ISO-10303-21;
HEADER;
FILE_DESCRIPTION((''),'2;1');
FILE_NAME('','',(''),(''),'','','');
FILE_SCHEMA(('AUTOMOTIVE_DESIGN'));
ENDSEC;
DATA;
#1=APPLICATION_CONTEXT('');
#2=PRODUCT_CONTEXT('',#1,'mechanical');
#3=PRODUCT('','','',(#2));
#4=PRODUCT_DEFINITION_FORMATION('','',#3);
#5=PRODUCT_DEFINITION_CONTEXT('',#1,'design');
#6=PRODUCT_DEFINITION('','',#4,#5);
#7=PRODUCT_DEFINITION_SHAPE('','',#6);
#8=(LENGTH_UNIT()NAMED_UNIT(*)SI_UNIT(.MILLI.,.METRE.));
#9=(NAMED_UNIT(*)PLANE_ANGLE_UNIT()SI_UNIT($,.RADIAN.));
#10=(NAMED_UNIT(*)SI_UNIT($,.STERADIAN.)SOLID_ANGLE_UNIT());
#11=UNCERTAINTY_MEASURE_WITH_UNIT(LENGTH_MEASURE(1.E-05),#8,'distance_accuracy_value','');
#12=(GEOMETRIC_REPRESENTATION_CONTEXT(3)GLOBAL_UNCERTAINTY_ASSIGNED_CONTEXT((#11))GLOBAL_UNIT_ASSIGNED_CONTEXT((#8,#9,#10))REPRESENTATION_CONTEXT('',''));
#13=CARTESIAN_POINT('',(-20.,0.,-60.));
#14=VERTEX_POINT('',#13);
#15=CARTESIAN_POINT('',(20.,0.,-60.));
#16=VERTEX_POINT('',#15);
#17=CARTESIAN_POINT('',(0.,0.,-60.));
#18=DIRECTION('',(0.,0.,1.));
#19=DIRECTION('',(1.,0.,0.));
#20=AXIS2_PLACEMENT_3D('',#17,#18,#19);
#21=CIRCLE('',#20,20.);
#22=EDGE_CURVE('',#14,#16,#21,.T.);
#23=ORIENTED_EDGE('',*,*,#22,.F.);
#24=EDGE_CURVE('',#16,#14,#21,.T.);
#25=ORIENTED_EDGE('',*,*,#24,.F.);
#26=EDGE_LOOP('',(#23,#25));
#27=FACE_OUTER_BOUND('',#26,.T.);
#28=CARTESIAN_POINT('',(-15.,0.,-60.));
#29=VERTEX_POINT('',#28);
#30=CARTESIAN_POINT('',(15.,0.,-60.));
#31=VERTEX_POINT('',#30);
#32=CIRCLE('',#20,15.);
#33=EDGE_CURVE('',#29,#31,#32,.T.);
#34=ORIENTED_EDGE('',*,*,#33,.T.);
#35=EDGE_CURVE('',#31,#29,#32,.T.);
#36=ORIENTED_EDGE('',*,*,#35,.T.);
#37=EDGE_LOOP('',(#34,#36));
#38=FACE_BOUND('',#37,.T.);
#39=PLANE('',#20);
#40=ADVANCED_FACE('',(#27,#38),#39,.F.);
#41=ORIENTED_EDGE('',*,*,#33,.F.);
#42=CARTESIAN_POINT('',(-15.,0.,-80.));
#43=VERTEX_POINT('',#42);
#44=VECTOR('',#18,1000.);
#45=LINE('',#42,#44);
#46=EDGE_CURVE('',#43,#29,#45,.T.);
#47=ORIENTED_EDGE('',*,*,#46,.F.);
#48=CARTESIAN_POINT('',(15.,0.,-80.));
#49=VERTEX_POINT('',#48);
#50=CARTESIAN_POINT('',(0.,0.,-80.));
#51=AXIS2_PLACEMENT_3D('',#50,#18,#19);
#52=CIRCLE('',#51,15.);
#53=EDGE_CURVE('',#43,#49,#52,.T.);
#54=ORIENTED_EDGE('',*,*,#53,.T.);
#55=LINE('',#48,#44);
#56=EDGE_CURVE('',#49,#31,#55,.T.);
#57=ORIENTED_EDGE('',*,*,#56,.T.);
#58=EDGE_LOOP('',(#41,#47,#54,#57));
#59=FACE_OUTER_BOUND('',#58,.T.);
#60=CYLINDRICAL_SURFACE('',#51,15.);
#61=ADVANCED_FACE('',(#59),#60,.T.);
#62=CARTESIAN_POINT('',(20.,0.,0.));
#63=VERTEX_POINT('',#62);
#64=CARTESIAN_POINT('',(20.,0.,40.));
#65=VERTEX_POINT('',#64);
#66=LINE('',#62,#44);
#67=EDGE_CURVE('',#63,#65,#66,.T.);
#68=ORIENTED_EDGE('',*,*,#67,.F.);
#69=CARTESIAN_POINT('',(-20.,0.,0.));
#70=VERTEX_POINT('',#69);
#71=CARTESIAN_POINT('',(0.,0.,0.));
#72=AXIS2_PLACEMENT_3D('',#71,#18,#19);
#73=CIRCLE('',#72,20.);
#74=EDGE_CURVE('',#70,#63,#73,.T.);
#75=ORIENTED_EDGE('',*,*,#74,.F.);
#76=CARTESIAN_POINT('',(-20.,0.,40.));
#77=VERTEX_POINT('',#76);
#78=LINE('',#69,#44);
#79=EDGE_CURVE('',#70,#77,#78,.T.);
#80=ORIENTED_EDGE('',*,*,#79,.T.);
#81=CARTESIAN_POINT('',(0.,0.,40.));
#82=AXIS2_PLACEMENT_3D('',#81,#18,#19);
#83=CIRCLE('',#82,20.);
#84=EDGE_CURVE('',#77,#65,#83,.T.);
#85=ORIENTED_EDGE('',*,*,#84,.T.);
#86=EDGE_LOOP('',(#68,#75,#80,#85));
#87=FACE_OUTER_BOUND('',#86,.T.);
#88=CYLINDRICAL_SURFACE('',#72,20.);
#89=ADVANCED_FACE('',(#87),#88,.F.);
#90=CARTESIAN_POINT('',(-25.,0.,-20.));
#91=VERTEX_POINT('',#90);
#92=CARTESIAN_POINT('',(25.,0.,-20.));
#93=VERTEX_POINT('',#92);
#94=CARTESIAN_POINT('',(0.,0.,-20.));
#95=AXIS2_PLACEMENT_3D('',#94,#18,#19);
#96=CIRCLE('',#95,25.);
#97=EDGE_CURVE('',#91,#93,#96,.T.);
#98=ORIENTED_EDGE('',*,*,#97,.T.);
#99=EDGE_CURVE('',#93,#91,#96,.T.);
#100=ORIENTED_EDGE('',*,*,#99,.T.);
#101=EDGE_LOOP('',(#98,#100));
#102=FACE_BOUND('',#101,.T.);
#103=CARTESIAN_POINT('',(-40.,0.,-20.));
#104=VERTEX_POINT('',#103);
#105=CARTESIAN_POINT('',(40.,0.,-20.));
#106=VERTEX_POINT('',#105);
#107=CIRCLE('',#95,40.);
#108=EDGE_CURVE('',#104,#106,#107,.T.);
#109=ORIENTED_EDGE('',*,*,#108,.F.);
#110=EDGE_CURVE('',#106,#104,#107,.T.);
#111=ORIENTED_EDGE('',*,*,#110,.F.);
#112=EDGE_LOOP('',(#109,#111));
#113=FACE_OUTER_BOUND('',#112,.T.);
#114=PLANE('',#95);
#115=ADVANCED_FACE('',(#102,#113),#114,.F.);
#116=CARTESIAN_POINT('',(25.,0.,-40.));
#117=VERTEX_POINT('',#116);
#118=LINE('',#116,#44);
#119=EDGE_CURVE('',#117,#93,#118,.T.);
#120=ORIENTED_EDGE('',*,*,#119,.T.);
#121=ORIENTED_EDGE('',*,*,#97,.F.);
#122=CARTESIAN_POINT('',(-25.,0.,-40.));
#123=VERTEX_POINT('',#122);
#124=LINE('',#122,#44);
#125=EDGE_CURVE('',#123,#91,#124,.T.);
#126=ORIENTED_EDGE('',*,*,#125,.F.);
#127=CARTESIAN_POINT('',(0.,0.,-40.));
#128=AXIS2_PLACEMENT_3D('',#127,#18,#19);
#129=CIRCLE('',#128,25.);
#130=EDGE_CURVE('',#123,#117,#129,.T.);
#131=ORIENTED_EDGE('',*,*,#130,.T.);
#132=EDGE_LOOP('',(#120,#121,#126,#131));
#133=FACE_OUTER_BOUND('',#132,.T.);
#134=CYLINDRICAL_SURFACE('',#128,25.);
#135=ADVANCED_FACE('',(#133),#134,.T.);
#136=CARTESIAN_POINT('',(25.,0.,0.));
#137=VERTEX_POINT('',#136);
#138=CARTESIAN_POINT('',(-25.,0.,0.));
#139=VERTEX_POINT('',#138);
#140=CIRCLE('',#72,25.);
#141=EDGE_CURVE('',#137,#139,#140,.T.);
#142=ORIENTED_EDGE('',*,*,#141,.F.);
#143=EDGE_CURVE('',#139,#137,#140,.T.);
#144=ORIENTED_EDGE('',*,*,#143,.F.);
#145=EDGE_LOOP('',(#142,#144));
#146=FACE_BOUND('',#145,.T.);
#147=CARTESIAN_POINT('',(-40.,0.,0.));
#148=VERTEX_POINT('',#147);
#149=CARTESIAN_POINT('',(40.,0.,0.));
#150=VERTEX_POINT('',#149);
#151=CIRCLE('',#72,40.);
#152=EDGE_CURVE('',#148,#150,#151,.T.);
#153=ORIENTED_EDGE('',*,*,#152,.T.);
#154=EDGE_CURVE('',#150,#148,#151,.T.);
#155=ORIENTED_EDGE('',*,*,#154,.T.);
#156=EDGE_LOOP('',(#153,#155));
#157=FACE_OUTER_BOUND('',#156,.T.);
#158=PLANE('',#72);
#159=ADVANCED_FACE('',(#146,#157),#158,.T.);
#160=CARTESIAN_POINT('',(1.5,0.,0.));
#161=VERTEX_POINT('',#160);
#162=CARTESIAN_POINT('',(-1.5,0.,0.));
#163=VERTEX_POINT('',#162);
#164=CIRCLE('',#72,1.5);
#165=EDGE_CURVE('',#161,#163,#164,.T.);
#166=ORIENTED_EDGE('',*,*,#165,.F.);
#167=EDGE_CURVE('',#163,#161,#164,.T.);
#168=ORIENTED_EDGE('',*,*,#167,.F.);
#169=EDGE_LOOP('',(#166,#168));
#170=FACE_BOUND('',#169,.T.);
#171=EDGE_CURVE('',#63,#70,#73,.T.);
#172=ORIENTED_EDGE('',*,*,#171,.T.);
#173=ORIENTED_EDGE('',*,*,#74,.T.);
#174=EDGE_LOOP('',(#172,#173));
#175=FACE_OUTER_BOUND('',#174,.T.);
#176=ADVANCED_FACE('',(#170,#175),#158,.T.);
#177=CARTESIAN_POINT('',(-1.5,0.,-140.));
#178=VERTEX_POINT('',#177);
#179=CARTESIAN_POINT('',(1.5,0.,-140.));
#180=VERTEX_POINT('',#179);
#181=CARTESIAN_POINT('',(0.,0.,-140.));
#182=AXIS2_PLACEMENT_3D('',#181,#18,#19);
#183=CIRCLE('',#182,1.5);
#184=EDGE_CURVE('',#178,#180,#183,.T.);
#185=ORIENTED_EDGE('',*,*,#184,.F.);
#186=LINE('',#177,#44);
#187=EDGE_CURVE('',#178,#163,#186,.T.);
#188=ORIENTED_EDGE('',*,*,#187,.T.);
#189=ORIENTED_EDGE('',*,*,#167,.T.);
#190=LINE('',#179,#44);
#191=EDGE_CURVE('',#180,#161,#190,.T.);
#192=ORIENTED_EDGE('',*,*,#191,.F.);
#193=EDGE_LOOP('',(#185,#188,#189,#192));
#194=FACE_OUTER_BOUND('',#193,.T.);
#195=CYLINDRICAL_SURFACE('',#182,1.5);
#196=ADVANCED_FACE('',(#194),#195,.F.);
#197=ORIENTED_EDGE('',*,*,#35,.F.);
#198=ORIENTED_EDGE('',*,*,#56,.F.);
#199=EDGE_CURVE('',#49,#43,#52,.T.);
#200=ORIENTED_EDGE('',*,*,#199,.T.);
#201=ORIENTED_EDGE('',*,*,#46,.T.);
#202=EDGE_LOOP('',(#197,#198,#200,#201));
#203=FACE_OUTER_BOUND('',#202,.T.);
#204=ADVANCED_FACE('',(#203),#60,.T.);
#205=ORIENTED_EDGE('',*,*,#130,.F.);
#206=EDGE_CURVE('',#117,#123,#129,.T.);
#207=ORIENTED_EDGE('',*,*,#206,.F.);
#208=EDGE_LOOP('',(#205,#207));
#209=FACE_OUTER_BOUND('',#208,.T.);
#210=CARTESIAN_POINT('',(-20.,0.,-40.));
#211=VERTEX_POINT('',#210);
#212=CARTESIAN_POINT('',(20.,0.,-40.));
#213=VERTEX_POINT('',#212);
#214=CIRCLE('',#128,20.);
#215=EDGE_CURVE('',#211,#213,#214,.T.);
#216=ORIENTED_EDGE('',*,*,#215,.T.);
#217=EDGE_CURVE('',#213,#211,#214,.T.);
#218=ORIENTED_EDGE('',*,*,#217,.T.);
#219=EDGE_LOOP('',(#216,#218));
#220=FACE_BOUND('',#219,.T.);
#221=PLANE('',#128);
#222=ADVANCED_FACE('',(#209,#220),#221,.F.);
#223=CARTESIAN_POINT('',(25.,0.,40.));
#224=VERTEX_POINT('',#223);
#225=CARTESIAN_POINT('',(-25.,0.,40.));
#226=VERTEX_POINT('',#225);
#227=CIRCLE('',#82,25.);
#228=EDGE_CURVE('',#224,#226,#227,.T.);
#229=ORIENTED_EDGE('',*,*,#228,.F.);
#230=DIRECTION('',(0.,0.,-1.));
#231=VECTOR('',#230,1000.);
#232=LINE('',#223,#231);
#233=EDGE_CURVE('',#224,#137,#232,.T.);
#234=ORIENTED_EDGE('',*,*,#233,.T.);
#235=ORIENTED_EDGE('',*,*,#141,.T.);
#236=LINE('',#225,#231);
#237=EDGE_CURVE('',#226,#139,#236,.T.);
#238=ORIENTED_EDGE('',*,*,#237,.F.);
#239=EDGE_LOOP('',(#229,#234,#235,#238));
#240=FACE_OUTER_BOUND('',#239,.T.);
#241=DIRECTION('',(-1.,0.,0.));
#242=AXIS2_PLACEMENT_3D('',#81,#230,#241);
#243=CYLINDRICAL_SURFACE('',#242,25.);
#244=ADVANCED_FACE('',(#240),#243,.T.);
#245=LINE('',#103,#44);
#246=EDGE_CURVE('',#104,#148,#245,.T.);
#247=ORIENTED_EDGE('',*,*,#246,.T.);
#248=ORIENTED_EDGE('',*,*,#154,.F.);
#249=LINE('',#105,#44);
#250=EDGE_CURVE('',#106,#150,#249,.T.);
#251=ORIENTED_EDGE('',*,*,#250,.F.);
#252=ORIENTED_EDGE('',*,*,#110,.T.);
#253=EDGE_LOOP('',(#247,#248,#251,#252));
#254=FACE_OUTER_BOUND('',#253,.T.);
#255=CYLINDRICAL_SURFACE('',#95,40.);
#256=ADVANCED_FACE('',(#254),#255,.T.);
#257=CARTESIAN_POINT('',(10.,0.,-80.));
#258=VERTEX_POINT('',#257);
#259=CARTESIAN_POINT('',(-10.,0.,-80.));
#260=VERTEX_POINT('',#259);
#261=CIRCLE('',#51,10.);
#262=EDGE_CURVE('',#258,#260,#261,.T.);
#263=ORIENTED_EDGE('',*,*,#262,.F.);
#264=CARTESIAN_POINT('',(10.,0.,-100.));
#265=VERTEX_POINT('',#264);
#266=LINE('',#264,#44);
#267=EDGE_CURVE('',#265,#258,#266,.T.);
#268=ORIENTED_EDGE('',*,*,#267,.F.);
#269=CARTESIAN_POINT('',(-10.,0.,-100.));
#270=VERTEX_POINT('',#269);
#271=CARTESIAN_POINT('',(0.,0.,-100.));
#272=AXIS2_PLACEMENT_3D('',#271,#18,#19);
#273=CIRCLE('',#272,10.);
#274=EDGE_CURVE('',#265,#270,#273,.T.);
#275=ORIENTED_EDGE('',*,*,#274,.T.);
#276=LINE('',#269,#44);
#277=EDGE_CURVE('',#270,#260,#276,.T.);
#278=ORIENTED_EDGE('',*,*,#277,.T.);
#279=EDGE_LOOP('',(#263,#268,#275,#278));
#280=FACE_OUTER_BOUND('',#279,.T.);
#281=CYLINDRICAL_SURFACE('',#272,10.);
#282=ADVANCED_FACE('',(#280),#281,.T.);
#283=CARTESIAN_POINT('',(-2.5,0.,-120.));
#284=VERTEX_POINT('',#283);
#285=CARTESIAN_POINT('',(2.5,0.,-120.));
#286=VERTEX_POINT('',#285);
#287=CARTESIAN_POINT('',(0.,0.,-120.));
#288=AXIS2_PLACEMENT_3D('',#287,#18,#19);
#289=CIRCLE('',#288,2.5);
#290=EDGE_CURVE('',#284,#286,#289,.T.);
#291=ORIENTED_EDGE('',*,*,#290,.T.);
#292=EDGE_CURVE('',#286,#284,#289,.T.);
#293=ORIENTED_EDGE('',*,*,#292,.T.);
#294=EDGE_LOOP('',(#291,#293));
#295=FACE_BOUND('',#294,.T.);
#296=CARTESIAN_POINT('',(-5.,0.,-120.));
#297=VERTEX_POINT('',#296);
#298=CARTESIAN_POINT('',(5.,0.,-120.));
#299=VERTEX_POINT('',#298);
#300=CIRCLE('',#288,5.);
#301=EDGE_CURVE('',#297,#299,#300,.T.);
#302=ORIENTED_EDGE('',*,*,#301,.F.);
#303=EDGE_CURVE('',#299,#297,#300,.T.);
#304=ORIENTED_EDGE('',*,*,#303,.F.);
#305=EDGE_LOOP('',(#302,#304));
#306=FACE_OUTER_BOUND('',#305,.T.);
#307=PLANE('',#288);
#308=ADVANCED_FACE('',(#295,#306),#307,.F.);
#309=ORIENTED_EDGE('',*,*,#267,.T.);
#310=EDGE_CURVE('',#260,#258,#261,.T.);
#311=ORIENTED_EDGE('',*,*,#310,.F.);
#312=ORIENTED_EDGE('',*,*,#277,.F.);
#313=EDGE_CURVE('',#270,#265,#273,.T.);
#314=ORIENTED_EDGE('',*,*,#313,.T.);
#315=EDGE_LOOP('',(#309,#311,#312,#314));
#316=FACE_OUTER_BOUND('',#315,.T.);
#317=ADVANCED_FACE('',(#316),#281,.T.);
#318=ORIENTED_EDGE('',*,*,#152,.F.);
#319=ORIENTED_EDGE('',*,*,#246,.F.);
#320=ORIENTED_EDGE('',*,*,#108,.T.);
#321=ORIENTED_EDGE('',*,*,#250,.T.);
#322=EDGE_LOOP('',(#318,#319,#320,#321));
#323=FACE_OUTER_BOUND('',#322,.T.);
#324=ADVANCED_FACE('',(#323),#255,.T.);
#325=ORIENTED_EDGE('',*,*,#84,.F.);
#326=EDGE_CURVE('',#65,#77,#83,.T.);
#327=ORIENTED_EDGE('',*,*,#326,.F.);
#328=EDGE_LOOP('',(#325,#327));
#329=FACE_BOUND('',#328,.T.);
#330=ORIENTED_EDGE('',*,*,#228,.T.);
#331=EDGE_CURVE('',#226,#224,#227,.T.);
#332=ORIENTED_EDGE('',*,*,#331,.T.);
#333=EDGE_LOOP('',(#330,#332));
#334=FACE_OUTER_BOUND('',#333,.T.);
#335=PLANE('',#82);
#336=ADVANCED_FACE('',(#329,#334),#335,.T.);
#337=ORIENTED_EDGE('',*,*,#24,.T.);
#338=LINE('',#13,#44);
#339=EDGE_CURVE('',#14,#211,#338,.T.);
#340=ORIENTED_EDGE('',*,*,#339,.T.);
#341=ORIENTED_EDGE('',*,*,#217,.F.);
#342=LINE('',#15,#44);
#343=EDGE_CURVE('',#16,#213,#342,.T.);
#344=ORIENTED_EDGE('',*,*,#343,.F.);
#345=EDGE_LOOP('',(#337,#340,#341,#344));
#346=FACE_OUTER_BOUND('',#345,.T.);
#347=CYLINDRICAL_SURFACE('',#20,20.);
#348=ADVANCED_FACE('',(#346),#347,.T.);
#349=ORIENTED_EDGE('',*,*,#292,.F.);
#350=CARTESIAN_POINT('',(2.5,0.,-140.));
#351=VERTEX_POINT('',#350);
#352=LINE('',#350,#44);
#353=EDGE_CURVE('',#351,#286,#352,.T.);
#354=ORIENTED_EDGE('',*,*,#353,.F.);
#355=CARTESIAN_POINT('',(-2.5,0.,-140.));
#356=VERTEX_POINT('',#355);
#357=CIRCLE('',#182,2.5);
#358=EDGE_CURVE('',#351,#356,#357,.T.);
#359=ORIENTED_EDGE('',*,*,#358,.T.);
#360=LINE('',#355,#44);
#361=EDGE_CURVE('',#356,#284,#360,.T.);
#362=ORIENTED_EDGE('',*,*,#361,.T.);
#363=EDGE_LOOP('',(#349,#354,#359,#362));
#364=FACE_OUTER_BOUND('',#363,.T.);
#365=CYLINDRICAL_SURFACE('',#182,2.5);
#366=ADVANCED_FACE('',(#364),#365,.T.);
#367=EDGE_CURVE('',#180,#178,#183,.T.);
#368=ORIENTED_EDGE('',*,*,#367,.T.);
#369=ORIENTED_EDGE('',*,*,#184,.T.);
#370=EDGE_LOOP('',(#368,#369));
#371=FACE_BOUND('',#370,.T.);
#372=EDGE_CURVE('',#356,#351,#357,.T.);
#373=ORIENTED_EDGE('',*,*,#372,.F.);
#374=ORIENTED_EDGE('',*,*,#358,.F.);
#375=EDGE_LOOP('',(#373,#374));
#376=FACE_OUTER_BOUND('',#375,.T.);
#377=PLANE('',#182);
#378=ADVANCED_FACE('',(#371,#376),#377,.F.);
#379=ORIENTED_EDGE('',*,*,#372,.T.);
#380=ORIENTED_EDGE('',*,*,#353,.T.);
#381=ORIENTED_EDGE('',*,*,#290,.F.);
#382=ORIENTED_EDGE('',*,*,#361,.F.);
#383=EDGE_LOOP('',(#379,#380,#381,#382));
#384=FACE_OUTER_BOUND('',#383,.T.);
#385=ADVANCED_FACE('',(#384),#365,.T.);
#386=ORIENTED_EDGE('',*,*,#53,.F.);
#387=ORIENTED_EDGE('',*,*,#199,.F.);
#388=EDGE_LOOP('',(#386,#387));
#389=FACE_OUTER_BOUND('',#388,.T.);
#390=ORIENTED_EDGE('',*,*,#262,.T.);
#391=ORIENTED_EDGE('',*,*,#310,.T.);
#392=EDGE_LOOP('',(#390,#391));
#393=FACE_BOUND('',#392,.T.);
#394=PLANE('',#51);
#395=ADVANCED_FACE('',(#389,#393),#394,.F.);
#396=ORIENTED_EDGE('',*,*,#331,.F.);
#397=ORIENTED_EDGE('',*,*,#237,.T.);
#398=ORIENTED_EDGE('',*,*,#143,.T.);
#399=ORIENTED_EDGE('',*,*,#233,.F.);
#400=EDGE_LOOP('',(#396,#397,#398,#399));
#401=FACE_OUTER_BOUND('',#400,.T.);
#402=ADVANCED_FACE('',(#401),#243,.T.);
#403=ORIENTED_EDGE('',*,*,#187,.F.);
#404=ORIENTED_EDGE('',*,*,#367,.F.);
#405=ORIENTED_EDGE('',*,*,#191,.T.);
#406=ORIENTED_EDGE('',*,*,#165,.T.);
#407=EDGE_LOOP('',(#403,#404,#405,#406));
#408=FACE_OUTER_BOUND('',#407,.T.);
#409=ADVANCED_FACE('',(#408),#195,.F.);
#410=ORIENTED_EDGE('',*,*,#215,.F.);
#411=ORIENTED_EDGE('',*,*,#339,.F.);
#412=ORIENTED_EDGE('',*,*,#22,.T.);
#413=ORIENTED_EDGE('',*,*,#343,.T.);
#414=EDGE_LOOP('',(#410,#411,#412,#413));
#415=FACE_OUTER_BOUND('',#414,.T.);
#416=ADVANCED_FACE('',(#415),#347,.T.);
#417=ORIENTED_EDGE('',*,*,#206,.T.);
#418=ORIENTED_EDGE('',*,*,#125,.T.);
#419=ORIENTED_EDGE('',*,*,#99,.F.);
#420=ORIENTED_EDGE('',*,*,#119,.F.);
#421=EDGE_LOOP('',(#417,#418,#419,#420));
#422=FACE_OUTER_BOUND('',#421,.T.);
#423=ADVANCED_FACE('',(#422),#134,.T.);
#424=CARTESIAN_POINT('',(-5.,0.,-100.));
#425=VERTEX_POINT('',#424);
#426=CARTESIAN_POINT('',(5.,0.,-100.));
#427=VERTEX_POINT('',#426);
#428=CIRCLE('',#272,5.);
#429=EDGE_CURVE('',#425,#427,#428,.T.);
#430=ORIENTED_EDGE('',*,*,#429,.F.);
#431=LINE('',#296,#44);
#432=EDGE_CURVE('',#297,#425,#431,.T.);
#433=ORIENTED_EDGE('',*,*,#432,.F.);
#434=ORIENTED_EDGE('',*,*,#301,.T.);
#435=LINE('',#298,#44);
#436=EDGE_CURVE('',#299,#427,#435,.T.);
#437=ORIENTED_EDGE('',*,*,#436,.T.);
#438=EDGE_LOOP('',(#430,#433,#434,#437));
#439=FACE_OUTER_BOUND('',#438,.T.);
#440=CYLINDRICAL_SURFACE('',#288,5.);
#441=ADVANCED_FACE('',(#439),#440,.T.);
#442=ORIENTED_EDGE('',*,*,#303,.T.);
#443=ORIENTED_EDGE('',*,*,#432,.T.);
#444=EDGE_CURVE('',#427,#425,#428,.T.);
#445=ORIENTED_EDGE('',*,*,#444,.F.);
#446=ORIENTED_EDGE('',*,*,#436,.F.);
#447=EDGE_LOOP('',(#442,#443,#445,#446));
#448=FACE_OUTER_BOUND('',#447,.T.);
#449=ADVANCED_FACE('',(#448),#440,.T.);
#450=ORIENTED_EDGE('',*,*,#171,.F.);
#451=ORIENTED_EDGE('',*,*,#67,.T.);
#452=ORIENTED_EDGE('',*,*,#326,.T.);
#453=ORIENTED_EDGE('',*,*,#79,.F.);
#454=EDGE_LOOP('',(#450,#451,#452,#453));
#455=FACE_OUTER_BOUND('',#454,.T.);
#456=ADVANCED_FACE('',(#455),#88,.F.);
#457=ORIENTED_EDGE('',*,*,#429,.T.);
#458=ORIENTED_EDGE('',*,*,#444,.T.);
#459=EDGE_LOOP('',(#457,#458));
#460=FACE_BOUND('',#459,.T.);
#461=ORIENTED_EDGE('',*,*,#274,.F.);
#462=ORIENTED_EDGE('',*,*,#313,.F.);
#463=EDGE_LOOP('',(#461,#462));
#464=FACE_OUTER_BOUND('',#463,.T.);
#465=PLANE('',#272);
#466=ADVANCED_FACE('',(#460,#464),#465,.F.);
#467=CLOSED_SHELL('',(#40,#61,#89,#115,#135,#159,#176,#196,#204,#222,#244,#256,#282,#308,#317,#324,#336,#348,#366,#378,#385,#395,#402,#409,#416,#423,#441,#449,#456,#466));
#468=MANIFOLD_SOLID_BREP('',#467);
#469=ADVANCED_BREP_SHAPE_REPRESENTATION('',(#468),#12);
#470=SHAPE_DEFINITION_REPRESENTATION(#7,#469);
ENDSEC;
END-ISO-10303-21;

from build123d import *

# Parameters (mm, degrees)
FLANGE_PROFILE_80_R    = 40
FLANGE_80_DEPTH        = 20
STEP_50_PROFILE_R      = 25
SHAFT_STEP_50_DEPTH    = 40
STEP_40_PROFILE_R      = 20
SHAFT_STEP_40_DEPTH    = 60
STEP_30_PROFILE_R      = 15
SHAFT_STEP_30_DEPTH    = 80
STEP_20_PROFILE_R      = 10
SHAFT_STEP_20_DEPTH    = 100
STEP_10_PROFILE_R      = 5
SHAFT_STEP_10_DEPTH    = 120
TIP_PIN_5_PROFILE_R    = 2.5
TIP_PIN_5_DEPTH        = 140
HUB_START              = 40
HUB_50_PROFILE_R       = 25
HUB_50_DEPTH           = 40
HUB_BORE_40_PROFILE_R  = 20
HUB_BORE_40_DEPTH      = 40
AXIAL_BORE_3_PROFILE_R = 1.5
AXIAL_BORE_3_DEPTH     = 140


with BuildPart() as part:
    # Flange Profile Ø80 → Flange Ø80 (new body)
    with BuildSketch(Plane.XY):
        Circle(FLANGE_PROFILE_80_R)
    extrude(amount=-FLANGE_80_DEPTH)

    # Step Ø50 Profile → Shaft Step Ø50 (add)
    with BuildSketch(Plane.XY):
        Circle(STEP_50_PROFILE_R)
    extrude(amount=-SHAFT_STEP_50_DEPTH)

    # Step Ø40 Profile → Shaft Step Ø40 (add)
    with BuildSketch(Plane.XY):
        Circle(STEP_40_PROFILE_R)
    extrude(amount=-SHAFT_STEP_40_DEPTH)

    # Step Ø30 Profile → Shaft Step Ø30 (add)
    with BuildSketch(Plane.XY):
        Circle(STEP_30_PROFILE_R)
    extrude(amount=-SHAFT_STEP_30_DEPTH)

    # Step Ø20 Profile → Shaft Step Ø20 (add)
    with BuildSketch(Plane.XY):
        Circle(STEP_20_PROFILE_R)
    extrude(amount=-SHAFT_STEP_20_DEPTH)

    # Step Ø10 Profile → Shaft Step Ø10 (add)
    with BuildSketch(Plane.XY):
        Circle(STEP_10_PROFILE_R)
    extrude(amount=-SHAFT_STEP_10_DEPTH)

    # Tip Pin Ø5 Profile → Tip Pin Ø5 (add)
    with BuildSketch(Plane.XY):
        Circle(TIP_PIN_5_PROFILE_R)
    extrude(amount=-TIP_PIN_5_DEPTH)

    # Hub Ø50 Profile → Hub Ø50 (add)
    with BuildSketch(Plane.XY.offset(HUB_START)):
        Circle(HUB_50_PROFILE_R)
    extrude(amount=-HUB_50_DEPTH)

    # Hub Bore Ø40 Profile → Hub Bore Ø40 (cut)
    with BuildSketch(Plane.XY.offset(40)):
        Circle(HUB_BORE_40_PROFILE_R)
    extrude(amount=-HUB_BORE_40_DEPTH, mode=Mode.SUBTRACT)

    # Axial Bore Ø3 Profile → Axial Bore Ø3 (cut)
    with BuildSketch(Plane.XY):
        Circle(AXIAL_BORE_3_PROFILE_R)
    extrude(amount=-AXIAL_BORE_3_DEPTH, mode=Mode.SUBTRACT)


solid = part.part
